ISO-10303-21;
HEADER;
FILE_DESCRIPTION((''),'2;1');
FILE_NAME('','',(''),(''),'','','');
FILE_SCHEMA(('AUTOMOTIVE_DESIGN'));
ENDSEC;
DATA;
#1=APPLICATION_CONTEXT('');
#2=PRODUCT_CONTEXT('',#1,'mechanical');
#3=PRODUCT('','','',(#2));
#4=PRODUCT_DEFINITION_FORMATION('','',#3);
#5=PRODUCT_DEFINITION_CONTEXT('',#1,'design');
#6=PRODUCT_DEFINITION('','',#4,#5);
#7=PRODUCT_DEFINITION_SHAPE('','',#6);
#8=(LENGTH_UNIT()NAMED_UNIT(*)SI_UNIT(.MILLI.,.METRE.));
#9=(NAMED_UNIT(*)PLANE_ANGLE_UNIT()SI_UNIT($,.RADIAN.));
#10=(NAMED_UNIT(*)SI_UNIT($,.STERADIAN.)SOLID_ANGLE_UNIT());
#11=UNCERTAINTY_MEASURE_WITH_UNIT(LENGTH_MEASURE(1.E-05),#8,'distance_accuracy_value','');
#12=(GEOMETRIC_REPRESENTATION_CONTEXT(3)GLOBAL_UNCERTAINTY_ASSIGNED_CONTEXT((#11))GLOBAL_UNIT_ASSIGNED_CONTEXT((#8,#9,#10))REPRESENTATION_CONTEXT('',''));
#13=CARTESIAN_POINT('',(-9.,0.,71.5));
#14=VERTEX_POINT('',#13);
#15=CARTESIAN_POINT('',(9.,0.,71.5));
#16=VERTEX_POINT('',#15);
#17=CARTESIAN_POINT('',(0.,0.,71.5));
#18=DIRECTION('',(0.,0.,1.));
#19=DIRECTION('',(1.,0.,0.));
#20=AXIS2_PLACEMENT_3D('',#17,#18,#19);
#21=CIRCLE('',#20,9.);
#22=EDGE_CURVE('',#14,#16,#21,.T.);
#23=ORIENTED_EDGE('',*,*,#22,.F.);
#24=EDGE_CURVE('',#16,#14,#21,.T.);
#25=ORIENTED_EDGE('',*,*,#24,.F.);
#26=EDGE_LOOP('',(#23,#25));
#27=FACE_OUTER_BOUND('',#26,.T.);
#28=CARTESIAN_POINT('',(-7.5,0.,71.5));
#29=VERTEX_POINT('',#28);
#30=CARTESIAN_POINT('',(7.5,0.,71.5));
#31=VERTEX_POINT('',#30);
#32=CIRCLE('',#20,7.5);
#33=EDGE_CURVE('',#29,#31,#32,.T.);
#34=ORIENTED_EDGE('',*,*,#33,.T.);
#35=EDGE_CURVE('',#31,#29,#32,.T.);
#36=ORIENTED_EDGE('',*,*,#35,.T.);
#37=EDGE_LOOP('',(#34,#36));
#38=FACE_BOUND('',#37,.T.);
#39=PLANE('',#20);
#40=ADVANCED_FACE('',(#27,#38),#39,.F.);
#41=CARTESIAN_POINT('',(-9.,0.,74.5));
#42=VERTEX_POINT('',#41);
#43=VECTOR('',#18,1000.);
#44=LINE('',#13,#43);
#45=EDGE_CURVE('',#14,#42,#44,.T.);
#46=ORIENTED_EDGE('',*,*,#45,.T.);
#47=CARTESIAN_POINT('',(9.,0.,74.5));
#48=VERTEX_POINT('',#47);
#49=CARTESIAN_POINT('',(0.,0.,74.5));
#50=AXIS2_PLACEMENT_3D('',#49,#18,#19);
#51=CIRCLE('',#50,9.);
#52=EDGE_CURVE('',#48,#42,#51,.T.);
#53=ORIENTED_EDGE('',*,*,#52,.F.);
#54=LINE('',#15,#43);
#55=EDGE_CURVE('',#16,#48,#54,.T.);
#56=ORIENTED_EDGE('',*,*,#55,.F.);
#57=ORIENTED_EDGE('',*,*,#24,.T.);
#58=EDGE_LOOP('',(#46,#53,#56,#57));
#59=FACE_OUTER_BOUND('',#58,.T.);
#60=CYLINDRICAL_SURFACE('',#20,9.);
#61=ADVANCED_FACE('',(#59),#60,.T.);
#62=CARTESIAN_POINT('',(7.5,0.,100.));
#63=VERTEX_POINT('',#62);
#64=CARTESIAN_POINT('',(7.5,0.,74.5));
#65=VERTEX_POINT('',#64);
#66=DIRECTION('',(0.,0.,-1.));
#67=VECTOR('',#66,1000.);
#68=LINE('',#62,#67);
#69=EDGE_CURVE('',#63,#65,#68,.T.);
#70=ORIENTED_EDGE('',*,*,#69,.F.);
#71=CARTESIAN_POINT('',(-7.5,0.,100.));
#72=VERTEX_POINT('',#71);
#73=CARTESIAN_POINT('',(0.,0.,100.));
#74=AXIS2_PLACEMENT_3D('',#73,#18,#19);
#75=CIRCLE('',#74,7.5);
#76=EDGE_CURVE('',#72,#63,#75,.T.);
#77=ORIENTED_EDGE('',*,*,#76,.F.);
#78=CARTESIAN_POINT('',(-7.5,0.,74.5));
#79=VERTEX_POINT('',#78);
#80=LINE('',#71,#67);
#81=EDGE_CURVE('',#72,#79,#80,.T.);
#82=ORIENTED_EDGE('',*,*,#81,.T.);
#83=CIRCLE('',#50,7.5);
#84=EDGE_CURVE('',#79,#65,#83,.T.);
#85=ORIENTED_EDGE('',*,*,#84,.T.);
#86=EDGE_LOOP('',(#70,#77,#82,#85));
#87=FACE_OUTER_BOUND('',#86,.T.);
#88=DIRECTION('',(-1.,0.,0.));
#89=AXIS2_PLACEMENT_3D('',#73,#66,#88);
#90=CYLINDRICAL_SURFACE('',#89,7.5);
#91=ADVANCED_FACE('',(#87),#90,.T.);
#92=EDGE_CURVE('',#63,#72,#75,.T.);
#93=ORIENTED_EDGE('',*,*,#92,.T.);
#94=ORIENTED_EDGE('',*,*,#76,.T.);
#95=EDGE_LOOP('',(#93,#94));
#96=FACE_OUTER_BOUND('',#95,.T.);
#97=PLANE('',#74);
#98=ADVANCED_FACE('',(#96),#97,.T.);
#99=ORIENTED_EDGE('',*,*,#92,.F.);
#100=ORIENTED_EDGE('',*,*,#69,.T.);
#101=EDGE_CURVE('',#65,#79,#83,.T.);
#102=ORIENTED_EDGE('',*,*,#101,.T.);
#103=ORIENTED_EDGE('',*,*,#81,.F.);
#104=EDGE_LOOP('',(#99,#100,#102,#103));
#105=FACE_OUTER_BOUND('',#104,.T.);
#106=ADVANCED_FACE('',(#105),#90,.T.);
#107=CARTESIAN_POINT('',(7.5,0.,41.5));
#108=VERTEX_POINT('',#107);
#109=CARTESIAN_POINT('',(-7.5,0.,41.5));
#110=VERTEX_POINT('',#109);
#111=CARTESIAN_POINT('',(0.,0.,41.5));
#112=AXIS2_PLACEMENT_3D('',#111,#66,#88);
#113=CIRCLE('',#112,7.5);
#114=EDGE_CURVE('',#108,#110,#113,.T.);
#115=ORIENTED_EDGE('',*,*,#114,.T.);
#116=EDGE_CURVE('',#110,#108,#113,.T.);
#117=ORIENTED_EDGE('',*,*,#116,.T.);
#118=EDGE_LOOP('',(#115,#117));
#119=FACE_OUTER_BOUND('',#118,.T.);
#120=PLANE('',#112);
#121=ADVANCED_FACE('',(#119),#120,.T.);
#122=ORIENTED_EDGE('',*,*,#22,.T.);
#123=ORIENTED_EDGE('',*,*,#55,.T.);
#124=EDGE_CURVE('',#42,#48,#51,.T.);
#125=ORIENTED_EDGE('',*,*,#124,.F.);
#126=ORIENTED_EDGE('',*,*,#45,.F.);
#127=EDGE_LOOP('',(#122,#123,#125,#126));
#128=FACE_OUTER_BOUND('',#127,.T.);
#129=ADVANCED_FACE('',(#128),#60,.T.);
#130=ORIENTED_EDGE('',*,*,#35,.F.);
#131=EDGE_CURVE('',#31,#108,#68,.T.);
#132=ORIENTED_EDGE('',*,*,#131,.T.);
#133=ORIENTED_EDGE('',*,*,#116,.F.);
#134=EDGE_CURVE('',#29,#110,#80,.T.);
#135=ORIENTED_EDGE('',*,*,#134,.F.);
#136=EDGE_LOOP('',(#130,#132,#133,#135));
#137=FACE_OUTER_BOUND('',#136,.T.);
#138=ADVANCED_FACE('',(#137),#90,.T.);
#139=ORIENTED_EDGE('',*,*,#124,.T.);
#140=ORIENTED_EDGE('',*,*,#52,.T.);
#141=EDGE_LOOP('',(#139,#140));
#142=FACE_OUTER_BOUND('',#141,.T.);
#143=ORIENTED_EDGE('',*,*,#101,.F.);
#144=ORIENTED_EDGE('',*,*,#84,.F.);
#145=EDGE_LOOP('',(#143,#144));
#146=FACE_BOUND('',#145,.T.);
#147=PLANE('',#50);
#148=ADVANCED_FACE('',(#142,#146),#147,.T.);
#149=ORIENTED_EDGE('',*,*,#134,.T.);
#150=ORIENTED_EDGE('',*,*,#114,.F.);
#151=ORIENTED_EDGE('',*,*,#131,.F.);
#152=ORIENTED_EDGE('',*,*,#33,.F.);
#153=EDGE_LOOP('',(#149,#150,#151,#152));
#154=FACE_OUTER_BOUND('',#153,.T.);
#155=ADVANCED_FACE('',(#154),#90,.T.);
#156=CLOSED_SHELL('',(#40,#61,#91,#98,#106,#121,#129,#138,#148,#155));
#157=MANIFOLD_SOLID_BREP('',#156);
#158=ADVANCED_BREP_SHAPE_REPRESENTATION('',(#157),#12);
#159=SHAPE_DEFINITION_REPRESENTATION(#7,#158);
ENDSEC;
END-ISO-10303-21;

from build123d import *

# Parameters (mm, degrees)
SKETCH_1_R          = 7.5
EXTRUDE_1_DEPTH     = 100
EXTRUDE_START       = -25.5
SKETCH_2_R          = 9
EXTRUDE_2_DEPTH     = 3
EXTRUDE_START_2     = -28.5
SKETCH_3_R          = 9
EXTRUDE_3_DEPTH     = 3
EXTRUDE_START_3     = 40
SKETCH_4_R          = 7.5
EXTRUDE_4_DEPTH     = 40
SKETCH_5_R          = 10
CUT_EXTRUDE_2_DEPTH = 81.5


with BuildPart() as part:
    # 草图1 → 凸台-拉伸1 (new body)
    with BuildSketch(Plane.XY):
        Circle(SKETCH_1_R)
    extrude(amount=EXTRUDE_1_DEPTH)

    # 草图2 → 凸台-拉伸2 (add)
    with BuildSketch(Plane.XY.offset(100).offset(EXTRUDE_START)):
        Circle(SKETCH_2_R)
    extrude(amount=-EXTRUDE_2_DEPTH)

    # 草图3 → 凸台-拉伸3 (add)
    with BuildSketch(Plane(origin=(0, 0, 0), x_dir=(-1, 0, 0), z_dir=(0, 0, -1)).offset(EXTRUDE_START_2)):
        with Locations(Location((0, 0, 0), (0, 0, 180))):
            Circle(SKETCH_3_R)
    extrude(amount=EXTRUDE_3_DEPTH)

    # 草图4 → 凸台-拉伸4 (add)
    with BuildSketch(Plane(origin=(0, 0, 0), x_dir=(-1, 0, 0), z_dir=(0, 0, -1)).offset(EXTRUDE_START_3)):
        Circle(SKETCH_4_R)
    extrude(amount=-EXTRUDE_4_DEPTH)

    # 草图5 → 切除-拉伸2 (cut)
    with BuildSketch(Plane(origin=(0, 0, -40), x_dir=(-1, 0, 0), z_dir=(0, 0, -1))):
        Circle(SKETCH_5_R)
    extrude(amount=-CUT_EXTRUDE_2_DEPTH, mode=Mode.SUBTRACT)


solid = part.part
